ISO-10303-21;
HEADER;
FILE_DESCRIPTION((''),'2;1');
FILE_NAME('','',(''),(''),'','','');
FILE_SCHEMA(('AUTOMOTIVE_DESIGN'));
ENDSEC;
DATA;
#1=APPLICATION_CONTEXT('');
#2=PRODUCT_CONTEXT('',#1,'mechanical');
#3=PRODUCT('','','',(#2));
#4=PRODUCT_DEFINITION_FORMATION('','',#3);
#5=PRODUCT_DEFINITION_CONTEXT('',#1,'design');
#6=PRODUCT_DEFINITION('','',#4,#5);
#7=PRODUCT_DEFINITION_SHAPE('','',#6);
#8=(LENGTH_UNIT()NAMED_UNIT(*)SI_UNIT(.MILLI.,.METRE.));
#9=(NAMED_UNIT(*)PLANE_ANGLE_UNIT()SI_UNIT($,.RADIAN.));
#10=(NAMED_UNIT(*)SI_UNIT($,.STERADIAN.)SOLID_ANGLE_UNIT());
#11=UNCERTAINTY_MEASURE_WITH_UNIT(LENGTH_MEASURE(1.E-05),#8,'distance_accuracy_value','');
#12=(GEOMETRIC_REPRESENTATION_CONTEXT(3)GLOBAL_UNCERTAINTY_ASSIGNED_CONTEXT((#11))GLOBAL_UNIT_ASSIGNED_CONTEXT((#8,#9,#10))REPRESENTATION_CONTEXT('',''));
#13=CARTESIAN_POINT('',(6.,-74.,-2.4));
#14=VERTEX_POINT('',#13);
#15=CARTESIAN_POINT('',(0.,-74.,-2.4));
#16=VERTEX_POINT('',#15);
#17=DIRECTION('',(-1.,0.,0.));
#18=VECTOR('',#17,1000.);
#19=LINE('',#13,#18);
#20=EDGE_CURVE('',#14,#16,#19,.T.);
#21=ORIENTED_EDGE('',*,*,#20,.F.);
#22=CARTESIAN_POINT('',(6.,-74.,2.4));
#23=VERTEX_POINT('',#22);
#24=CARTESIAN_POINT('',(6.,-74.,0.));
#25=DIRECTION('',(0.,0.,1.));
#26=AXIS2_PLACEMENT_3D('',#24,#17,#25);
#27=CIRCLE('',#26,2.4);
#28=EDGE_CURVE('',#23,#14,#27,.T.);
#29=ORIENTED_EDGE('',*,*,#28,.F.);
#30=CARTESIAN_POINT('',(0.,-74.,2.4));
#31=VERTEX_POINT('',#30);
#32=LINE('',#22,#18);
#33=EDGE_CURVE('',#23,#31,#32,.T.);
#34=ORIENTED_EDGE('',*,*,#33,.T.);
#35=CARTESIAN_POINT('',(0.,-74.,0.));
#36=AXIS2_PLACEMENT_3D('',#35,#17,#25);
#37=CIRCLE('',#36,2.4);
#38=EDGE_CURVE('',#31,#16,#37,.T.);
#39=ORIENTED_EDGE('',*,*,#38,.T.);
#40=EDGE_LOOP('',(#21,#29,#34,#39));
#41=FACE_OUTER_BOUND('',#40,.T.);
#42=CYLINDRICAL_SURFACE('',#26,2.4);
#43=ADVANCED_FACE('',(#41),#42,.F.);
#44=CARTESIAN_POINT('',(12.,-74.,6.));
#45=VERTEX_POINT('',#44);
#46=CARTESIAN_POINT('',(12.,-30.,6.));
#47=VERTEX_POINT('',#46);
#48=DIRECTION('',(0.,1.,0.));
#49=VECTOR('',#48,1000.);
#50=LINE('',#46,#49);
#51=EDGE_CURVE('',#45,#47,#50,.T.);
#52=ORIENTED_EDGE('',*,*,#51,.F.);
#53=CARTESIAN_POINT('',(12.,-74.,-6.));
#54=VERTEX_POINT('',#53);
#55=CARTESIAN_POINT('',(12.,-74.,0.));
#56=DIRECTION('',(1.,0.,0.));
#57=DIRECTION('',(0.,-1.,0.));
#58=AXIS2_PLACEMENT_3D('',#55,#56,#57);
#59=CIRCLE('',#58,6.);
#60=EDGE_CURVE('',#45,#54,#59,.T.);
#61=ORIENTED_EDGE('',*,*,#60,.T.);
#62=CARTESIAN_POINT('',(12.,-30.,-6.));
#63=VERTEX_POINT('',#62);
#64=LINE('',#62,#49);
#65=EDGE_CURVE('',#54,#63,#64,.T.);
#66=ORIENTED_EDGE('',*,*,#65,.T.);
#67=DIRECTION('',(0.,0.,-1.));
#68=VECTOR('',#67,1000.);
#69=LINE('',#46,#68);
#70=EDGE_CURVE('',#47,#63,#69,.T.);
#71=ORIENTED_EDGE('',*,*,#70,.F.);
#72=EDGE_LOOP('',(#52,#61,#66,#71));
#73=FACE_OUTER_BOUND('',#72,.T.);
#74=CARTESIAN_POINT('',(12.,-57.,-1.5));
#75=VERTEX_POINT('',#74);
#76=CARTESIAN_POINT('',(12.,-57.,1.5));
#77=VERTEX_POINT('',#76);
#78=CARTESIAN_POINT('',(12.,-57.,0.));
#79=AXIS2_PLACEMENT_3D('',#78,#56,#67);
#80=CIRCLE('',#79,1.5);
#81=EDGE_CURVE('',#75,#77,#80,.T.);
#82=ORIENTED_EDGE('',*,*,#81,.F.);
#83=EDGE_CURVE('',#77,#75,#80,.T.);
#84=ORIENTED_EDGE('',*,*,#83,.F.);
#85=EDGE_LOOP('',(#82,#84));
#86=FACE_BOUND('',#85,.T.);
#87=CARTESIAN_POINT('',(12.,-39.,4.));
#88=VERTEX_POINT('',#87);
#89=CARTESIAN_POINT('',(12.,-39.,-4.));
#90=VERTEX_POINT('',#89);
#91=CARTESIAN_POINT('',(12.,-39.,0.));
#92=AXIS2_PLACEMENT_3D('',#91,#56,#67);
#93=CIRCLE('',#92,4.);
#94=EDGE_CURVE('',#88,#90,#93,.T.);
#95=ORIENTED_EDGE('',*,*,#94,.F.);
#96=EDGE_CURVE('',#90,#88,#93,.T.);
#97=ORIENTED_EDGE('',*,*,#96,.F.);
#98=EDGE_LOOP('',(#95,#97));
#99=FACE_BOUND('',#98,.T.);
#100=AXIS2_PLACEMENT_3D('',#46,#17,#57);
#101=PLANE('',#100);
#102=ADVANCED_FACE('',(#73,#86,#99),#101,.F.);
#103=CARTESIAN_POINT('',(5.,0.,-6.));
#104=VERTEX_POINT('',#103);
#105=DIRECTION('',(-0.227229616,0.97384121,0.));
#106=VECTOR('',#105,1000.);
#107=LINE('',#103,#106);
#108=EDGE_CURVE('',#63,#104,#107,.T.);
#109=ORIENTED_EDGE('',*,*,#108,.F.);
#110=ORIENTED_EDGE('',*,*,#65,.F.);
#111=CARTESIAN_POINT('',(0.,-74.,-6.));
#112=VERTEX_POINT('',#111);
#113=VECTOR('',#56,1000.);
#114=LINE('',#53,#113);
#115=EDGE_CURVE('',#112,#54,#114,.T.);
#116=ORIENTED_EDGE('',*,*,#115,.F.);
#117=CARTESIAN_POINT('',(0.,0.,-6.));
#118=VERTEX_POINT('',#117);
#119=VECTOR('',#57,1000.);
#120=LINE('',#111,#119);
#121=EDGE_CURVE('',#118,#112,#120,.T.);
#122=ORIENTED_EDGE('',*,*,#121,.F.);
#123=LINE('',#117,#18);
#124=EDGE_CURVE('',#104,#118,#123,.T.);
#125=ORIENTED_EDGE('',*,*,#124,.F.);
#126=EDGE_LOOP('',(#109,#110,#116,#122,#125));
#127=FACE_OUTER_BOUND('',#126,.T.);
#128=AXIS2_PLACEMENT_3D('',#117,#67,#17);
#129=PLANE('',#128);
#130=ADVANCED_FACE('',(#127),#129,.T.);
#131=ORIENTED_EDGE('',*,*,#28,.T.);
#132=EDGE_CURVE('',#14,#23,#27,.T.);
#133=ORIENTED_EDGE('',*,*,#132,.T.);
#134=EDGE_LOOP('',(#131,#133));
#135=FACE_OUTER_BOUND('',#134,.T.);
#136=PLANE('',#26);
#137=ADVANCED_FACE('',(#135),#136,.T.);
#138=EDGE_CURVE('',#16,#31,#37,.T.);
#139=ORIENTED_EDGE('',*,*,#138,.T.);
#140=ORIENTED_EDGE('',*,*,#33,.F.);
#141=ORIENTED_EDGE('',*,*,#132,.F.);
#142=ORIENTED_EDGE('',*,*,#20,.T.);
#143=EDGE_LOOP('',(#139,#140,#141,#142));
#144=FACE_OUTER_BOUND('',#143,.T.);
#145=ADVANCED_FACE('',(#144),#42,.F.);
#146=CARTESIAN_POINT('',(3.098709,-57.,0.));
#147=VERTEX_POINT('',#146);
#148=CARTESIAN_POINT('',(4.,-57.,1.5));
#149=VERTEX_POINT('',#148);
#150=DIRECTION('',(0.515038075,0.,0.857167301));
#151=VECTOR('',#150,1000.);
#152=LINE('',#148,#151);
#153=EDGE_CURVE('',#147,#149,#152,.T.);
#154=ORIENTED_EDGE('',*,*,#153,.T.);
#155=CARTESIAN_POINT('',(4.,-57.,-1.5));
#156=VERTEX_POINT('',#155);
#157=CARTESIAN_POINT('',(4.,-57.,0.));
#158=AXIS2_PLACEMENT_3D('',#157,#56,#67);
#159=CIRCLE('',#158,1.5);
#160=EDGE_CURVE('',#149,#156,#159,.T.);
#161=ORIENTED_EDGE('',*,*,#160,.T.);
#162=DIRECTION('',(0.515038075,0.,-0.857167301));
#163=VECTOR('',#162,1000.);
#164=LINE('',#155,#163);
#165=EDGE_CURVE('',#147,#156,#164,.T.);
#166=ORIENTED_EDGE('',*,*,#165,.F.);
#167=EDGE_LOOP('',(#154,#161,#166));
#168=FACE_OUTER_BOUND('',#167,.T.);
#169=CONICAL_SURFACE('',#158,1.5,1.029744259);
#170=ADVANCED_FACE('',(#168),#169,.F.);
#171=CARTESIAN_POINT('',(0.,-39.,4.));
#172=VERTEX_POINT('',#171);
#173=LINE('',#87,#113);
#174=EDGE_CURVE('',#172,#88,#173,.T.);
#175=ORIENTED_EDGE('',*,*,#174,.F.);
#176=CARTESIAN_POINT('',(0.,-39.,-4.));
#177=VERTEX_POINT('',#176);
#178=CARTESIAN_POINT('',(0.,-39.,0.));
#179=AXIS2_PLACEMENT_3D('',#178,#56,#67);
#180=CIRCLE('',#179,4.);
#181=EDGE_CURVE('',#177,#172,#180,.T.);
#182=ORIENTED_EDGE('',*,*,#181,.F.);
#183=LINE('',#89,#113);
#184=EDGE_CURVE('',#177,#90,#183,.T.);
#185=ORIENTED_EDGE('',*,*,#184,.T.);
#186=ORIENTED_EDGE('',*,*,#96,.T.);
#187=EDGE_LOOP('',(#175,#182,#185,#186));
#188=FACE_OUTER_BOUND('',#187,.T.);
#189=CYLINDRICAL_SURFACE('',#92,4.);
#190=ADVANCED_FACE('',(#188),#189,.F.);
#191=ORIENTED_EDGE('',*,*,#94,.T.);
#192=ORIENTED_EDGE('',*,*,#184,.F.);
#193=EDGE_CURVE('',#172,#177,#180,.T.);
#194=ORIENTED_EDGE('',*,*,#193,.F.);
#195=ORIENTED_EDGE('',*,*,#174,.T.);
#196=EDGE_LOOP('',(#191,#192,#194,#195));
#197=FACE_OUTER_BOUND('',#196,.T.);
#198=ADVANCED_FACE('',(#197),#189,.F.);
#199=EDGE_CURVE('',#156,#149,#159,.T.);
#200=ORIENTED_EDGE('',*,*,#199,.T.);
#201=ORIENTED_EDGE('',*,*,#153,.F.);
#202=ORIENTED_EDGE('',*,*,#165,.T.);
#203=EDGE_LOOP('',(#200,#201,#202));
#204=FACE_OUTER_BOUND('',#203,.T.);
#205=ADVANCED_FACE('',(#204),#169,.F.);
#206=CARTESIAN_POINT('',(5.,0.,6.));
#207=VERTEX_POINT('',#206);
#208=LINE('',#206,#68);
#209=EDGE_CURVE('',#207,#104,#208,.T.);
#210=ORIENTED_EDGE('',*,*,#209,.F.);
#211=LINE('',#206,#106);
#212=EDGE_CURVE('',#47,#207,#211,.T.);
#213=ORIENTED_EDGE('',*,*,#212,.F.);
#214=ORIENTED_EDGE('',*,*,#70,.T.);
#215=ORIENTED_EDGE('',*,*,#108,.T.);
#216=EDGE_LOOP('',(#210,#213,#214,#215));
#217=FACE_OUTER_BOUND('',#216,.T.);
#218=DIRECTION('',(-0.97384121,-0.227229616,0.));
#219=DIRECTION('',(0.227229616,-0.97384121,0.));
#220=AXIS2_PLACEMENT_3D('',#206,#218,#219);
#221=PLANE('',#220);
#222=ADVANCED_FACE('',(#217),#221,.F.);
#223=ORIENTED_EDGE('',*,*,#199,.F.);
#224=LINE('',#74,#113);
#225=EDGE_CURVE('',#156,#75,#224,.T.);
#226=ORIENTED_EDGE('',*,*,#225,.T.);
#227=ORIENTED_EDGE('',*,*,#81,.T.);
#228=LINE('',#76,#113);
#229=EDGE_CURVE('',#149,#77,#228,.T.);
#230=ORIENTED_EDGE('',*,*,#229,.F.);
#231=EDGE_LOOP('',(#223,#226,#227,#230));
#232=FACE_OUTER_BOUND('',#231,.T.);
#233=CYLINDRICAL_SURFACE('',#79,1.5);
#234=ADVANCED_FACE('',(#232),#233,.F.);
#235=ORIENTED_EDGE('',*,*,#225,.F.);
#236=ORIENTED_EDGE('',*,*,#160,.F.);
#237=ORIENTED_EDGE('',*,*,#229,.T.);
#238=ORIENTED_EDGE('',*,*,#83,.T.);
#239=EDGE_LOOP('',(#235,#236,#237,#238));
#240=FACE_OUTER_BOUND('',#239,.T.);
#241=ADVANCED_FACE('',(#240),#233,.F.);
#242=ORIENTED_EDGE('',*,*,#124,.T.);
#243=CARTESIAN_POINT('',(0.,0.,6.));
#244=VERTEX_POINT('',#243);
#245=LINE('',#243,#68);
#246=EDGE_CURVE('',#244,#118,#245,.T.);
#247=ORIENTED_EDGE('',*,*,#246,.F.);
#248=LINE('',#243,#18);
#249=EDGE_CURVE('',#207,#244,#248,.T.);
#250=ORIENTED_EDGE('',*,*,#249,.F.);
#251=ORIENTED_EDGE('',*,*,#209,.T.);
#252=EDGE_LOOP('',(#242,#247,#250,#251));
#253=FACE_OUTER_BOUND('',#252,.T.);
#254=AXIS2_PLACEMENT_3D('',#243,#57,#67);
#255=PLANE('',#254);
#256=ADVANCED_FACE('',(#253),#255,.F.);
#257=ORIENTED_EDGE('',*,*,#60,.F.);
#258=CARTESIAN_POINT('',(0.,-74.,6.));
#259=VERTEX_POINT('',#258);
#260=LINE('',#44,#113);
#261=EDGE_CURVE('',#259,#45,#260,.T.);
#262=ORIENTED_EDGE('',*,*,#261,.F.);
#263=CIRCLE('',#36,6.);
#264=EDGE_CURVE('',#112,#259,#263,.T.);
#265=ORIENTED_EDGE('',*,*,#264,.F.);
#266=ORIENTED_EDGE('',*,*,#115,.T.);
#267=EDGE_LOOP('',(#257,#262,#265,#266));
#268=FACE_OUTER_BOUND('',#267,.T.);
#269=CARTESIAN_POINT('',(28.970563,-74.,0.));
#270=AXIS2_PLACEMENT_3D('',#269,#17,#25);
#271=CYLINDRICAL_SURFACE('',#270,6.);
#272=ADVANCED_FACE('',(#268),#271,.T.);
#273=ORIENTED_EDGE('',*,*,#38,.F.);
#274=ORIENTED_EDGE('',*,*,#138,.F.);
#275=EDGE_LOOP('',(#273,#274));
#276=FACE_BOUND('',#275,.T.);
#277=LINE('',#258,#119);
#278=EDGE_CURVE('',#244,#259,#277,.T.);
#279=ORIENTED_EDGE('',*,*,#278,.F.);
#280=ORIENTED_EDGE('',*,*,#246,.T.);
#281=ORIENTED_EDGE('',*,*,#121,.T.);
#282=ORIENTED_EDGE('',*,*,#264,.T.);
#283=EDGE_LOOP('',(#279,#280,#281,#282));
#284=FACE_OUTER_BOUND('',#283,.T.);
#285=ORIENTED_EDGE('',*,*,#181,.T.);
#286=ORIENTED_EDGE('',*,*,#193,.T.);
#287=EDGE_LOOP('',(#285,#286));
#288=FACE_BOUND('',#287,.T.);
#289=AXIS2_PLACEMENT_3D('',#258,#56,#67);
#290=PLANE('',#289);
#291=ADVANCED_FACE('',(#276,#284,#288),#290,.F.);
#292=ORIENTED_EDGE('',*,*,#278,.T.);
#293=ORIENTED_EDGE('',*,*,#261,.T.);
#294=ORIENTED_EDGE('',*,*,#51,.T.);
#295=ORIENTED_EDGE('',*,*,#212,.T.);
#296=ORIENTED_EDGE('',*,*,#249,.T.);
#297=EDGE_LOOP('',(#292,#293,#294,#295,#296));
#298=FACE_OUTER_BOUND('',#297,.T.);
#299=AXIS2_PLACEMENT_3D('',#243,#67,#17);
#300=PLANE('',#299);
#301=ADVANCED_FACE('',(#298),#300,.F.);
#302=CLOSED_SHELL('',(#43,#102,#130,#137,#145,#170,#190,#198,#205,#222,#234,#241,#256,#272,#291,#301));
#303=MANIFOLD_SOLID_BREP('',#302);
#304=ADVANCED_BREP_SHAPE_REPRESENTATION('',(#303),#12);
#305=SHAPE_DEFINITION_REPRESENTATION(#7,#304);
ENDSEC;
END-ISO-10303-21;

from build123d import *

# Parameters (mm, degrees)
JAW_BODY_12MM_DEPTH       = 6
END_BOSS_SKETCH_R         = 6
END_BOSS_DEPTH            = 12
CUT_4_8_SKETCH_R          = 2.4
CUT_4_8_X_6_DEPTH         = 6
TAPPED_HOLE_M8X1_25_D     = 8
TAPPED_HOLE_M8X1_25_DEPTH = 19.75
TAPPED_HOLE_M8X1_25_TIP   = 2.403442476
TAPPED_HOLE_M3X0_5_D      = 3
TAPPED_HOLE_M3X0_5_DEPTH  = 8
TAPPED_HOLE_M3X0_5_TIP    = 0.901290929


with BuildPart() as part:
    # Jaw Profile Sketch → Jaw Body 12mm (new, symmetric)
    with BuildSketch(Plane.XY):
        Polygon((0, 0), (5, 0), (12, -30), (12, -74), (0, -74), align=None)
    extrude(amount=JAW_BODY_12MM_DEPTH, both=True)

    # End Boss Sketch → End Boss (add)
    with BuildSketch(Plane.ZY):
        with Locations((0, -74)):
            Circle(END_BOSS_SKETCH_R)
    extrude(amount=-END_BOSS_DEPTH)

    # Cut Ø4.8 Sketch → Cut Ø4.8 x 6 (cut)
    with BuildSketch(Plane.ZY):
        with Locations((0, -74)):
            Circle(CUT_4_8_SKETCH_R)
    extrude(amount=-CUT_4_8_X_6_DEPTH, mode=Mode.SUBTRACT)

    # Tapped Hole M8x1.25
    with Locations(Plane(origin=(12, -39, 0), x_dir=(0, 1, 0), z_dir=(1, 0, 0))):
        with Locations((0, 0)):
            Hole(TAPPED_HOLE_M8X1_25_D / 2, depth=TAPPED_HOLE_M8X1_25_DEPTH)
            with Locations((0, 0, -(TAPPED_HOLE_M8X1_25_DEPTH + TAPPED_HOLE_M8X1_25_TIP / 2))):  # 118° drill point
                Cone(0, TAPPED_HOLE_M8X1_25_D / 2, TAPPED_HOLE_M8X1_25_TIP, mode=Mode.SUBTRACT)

    # Tapped Hole M3x0.5
    with Locations(Plane(origin=(12, -57, 0), x_dir=(0, 1, 0), z_dir=(1, 0, 0))):
        with Locations((0, 0)):
            Hole(TAPPED_HOLE_M3X0_5_D / 2, depth=TAPPED_HOLE_M3X0_5_DEPTH)
            with Locations((0, 0, -(TAPPED_HOLE_M3X0_5_DEPTH + TAPPED_HOLE_M3X0_5_TIP / 2))):  # 118° drill point
                Cone(0, TAPPED_HOLE_M3X0_5_D / 2, TAPPED_HOLE_M3X0_5_TIP, mode=Mode.SUBTRACT)


solid = part.part
